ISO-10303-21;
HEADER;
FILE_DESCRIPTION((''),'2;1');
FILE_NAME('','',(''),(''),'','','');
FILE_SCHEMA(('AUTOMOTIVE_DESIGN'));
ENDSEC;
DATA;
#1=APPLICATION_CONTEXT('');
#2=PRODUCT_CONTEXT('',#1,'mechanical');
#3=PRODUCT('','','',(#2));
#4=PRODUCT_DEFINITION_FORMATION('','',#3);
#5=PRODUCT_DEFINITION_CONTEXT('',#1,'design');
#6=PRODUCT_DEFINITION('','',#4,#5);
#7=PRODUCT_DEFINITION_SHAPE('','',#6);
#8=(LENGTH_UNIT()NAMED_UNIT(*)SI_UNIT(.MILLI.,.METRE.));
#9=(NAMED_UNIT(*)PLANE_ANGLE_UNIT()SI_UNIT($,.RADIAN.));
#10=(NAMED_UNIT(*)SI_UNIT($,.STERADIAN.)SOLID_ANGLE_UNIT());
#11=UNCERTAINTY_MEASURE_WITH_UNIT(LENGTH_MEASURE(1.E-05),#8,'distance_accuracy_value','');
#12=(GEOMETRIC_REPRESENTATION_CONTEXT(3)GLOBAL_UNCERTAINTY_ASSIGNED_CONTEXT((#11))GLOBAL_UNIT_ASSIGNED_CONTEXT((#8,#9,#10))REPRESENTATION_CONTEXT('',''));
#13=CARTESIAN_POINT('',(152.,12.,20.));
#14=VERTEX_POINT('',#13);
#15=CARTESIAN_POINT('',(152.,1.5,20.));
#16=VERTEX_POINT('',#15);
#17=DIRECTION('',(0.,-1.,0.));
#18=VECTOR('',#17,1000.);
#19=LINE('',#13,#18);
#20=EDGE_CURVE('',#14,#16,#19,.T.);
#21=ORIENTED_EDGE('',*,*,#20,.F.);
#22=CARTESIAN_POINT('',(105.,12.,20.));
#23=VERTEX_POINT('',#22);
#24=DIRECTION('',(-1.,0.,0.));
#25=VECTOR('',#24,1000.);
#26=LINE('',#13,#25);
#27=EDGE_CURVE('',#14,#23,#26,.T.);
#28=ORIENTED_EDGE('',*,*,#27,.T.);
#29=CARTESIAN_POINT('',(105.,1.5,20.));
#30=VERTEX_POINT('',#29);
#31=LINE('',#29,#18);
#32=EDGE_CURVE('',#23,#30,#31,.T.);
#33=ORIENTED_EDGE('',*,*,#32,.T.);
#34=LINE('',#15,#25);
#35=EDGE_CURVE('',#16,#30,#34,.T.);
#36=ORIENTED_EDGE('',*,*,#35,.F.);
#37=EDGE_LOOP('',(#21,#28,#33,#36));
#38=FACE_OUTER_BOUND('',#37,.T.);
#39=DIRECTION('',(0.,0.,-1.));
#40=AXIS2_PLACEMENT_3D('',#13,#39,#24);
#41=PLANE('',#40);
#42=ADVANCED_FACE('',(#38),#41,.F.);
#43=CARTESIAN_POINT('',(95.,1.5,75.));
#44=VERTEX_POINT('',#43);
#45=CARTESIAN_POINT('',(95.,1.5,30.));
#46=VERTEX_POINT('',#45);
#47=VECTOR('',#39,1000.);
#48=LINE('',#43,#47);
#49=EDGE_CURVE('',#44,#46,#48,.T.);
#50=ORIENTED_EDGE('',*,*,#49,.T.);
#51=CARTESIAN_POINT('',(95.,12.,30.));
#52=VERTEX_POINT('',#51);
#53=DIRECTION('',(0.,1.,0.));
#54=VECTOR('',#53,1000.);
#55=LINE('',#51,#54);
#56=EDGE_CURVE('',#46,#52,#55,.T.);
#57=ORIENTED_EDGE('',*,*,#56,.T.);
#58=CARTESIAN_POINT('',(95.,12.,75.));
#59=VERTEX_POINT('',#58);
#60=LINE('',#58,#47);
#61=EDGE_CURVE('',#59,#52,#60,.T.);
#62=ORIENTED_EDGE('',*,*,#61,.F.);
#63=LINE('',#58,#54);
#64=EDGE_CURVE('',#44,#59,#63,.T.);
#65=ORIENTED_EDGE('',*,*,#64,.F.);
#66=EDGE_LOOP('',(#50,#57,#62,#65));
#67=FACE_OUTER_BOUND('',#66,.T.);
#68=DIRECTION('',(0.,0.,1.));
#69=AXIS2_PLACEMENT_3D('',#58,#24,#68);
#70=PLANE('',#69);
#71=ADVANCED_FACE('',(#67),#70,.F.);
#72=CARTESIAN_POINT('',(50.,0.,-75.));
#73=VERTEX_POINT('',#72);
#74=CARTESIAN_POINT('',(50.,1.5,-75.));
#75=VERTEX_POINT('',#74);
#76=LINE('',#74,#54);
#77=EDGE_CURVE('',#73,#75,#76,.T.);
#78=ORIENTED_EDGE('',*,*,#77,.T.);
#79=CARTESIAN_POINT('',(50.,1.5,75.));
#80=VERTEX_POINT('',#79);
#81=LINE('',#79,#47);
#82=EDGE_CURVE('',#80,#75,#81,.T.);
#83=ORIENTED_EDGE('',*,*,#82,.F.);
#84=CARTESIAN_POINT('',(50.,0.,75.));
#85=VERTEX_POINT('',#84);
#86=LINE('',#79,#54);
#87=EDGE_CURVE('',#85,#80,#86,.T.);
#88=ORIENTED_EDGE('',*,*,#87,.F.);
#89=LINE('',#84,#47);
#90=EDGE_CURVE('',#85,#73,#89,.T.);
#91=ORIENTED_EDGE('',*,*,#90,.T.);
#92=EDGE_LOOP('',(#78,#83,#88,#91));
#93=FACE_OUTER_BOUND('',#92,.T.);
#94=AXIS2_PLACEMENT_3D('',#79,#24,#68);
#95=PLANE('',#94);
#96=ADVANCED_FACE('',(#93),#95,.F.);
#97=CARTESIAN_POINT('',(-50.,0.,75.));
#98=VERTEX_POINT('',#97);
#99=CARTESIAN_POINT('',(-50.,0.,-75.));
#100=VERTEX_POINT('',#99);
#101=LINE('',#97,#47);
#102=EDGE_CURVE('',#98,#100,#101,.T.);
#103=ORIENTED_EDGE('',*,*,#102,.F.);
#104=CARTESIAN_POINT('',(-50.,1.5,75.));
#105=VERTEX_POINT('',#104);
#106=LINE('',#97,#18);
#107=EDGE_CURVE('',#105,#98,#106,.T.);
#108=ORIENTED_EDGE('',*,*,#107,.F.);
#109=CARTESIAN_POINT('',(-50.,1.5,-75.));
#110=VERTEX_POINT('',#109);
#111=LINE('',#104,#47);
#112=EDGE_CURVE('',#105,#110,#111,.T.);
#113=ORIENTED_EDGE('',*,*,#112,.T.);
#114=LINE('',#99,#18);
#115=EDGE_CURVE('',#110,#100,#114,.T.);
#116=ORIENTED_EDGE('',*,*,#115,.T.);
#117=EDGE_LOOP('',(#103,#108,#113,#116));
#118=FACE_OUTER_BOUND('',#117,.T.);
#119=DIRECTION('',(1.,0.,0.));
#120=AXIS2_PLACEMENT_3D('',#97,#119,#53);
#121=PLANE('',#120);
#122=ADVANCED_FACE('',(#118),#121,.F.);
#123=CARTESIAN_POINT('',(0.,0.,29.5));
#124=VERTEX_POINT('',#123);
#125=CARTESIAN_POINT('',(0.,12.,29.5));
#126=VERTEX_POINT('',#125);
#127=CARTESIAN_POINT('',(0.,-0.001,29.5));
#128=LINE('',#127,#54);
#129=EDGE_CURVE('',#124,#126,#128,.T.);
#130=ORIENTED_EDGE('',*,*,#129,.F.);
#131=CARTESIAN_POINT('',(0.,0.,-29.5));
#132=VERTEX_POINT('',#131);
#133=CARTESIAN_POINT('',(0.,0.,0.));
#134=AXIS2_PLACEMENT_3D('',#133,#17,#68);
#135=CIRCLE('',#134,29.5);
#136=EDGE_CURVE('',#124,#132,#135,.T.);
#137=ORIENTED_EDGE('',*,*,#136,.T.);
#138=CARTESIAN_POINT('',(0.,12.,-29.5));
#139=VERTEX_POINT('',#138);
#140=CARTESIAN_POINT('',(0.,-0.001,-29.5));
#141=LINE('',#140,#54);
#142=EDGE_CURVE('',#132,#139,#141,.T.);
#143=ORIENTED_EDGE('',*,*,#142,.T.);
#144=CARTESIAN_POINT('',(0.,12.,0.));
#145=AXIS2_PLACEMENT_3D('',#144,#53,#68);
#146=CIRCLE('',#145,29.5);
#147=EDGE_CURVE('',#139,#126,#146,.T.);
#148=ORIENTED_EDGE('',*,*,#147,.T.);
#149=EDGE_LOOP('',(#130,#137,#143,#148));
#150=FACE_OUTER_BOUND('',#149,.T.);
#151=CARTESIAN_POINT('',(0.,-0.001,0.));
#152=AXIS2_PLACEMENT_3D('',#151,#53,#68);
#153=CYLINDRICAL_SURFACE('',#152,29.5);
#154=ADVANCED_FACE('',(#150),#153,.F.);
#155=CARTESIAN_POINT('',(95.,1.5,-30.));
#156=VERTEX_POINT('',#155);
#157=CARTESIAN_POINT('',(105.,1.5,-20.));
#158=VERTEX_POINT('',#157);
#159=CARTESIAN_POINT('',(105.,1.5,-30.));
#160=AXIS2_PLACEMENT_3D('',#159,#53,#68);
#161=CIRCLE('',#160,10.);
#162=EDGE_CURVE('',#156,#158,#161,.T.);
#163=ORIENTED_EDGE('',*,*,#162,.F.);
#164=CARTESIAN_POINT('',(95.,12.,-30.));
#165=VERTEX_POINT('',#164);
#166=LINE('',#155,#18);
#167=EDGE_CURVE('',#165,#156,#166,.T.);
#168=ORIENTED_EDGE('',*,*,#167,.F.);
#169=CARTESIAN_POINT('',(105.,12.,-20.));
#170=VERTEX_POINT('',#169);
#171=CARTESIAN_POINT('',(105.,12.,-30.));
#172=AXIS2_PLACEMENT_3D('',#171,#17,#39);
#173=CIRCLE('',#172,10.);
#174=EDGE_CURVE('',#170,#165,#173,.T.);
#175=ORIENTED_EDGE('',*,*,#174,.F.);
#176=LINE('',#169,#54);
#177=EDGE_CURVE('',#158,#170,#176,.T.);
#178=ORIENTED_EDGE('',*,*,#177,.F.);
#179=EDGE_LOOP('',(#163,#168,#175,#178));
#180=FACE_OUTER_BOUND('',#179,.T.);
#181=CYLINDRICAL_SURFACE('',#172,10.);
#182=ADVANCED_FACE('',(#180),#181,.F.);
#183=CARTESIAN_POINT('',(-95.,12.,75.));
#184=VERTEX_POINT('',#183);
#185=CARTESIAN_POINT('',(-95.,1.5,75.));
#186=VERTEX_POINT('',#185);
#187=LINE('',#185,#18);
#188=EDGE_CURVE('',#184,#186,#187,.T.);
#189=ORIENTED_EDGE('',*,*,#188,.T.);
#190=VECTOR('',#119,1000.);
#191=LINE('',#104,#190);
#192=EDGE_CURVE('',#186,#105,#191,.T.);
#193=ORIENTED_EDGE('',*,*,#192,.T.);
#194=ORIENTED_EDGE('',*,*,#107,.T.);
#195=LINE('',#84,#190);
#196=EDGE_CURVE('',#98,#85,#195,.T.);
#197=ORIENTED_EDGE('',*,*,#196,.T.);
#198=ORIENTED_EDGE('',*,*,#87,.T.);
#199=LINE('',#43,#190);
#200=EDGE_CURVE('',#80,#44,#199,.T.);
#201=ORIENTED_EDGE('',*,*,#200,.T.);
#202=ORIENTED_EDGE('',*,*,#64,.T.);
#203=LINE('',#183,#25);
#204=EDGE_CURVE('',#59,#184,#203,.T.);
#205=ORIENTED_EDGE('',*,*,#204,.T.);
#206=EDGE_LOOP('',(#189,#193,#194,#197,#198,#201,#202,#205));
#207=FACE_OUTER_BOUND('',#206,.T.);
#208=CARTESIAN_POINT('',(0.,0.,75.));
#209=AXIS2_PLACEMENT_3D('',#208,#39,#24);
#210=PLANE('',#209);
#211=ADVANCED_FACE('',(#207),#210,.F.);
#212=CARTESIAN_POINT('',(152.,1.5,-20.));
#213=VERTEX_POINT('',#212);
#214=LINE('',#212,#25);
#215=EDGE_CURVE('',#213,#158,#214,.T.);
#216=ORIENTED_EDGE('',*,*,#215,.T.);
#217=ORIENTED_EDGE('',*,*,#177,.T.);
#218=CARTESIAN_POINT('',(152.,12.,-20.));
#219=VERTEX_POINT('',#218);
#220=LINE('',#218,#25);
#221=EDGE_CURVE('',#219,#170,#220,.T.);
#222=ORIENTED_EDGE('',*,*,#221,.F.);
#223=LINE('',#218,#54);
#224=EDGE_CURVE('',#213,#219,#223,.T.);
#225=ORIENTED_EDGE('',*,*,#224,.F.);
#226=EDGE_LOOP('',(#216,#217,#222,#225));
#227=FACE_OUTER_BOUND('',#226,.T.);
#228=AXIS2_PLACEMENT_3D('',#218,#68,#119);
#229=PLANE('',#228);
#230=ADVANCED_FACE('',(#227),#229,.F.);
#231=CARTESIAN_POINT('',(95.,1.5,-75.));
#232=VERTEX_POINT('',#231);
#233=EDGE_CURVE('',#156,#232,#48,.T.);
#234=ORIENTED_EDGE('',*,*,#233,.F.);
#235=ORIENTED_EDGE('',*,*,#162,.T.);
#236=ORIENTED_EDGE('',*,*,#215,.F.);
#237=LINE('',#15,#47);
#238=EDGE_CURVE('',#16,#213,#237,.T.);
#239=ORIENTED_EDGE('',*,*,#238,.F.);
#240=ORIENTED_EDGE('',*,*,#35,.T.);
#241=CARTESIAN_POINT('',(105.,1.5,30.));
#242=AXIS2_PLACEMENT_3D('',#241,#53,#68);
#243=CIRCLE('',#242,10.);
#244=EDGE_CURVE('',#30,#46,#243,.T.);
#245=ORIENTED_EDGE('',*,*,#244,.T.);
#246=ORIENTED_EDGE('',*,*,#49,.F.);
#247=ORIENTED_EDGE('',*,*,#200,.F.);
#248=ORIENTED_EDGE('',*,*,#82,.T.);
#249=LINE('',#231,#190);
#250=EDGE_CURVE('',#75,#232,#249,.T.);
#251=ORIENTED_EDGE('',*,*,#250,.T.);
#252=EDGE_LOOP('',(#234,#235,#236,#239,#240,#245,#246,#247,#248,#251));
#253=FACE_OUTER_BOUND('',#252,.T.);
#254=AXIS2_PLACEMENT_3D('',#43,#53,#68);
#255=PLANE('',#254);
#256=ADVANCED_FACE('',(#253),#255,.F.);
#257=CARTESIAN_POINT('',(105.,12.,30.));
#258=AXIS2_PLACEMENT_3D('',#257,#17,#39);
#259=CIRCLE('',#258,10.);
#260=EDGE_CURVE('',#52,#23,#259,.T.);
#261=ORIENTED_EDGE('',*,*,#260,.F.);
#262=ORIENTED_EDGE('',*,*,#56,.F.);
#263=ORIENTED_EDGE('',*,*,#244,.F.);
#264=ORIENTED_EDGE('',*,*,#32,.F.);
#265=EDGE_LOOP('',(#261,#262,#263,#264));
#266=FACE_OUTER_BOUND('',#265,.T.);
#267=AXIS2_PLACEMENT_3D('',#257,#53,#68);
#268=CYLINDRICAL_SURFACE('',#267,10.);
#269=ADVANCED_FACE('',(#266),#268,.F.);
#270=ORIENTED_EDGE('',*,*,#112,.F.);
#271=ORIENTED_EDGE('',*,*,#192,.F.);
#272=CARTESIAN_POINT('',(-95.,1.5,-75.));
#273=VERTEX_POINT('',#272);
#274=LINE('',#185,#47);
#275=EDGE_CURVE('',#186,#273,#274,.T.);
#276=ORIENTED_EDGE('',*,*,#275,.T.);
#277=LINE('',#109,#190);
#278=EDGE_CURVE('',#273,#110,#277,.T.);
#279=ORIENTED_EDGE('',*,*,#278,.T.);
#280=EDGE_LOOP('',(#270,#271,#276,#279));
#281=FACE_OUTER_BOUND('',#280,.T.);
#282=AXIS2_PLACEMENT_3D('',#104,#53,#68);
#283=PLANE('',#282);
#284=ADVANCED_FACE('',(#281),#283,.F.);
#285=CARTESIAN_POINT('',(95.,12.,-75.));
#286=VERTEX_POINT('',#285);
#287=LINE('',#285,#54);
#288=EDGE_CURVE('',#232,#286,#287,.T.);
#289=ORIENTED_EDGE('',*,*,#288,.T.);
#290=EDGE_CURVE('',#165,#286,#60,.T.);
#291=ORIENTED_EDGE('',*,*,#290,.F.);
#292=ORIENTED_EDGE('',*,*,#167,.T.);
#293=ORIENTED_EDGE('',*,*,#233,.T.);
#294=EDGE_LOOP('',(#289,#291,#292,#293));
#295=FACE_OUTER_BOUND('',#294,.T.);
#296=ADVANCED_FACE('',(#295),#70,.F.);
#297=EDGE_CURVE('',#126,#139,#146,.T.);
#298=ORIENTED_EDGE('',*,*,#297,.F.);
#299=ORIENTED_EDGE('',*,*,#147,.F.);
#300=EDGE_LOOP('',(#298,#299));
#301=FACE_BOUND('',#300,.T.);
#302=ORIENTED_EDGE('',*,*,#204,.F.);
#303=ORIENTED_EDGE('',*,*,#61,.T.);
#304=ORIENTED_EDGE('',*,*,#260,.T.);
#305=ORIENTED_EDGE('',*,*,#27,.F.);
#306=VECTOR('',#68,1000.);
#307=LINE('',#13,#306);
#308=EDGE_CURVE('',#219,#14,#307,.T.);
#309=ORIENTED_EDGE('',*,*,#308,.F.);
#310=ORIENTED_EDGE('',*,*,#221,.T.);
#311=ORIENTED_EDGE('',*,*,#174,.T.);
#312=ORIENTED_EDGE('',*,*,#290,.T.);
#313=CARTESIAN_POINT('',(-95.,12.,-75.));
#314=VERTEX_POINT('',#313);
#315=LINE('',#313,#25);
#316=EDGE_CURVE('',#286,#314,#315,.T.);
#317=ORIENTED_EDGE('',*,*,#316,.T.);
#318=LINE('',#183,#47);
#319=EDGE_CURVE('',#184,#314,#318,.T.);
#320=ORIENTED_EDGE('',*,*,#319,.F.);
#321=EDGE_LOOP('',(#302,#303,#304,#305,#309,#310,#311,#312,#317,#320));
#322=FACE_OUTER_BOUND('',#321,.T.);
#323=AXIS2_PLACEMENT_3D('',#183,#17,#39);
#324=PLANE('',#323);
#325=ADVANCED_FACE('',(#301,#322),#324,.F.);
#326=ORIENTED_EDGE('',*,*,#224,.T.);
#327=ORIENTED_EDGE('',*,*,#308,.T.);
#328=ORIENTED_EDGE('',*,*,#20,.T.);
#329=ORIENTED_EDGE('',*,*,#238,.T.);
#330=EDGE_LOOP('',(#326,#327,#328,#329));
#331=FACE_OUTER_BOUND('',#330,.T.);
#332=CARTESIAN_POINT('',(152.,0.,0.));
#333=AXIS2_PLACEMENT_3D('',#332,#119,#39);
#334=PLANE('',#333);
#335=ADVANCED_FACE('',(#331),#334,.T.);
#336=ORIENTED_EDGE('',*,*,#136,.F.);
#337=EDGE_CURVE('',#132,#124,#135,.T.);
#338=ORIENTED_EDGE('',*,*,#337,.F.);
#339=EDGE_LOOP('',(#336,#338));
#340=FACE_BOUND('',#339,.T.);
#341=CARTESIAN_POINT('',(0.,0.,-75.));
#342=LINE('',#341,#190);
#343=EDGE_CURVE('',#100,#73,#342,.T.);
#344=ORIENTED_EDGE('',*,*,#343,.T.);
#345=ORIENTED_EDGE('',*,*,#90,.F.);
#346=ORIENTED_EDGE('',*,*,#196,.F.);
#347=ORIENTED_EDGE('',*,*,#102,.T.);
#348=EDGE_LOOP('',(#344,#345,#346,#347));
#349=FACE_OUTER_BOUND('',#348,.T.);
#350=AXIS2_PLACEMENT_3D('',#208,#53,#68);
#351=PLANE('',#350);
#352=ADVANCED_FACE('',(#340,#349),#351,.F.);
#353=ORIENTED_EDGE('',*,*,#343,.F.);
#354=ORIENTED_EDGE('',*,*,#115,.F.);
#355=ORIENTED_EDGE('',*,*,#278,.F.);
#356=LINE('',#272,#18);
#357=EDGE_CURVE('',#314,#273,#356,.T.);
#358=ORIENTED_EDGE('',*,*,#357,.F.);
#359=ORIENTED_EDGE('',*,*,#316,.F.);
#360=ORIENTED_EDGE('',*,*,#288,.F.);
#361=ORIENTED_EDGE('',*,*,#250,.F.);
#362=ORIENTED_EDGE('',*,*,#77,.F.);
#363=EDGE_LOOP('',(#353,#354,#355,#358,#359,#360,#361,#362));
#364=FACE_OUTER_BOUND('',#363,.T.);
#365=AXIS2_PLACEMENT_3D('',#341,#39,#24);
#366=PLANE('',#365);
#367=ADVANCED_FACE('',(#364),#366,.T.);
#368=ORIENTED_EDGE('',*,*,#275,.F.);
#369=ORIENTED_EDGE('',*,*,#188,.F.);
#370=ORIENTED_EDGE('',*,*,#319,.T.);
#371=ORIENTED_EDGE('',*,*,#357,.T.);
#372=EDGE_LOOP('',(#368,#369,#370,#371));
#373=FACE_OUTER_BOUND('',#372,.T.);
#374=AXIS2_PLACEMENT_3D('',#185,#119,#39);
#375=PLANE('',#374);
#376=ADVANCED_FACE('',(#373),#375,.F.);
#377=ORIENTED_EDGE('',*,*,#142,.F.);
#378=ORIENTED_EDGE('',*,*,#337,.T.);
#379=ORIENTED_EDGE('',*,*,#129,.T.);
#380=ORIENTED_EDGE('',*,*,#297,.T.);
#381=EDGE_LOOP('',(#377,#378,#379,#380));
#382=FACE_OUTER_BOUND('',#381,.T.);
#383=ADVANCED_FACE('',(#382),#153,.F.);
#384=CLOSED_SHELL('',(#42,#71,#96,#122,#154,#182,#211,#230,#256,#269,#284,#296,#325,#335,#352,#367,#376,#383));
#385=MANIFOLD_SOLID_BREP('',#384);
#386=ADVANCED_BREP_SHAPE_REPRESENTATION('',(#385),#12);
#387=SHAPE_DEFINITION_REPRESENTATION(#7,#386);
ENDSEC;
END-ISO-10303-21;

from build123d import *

# Parameters (mm, degrees)
EXTRUDE_1_DEPTH     = 75
CUT_EXTRUDE_1_REACH = 123.631
SKETCH_2_R          = 29.5
SKETCH_4_W          = 40
SKETCH_4_H          = 10.5
EXTRUDE_2_DEPTH     = 57
FILLET_1_R          = 10


with BuildPart() as part:
    # 草图1 → 凸台-拉伸1 (new, symmetric)
    with BuildSketch(Plane.XY):
        Polygon((0, 0), (-50, 0), (-50, 1.5), (-95, 1.5), (-95, 12), (95, 12), (95, 1.5), (50, 1.5), (50, 0), align=None)
    extrude(amount=EXTRUDE_1_DEPTH, both=True)

    # 草图2 → 切除-拉伸1 (cut, up to next)
    with BuildSketch(Plane(origin=(0, 12, 0), x_dir=(1, 0, 0), z_dir=(0, 1, 0)), mode=Mode.PRIVATE) as cut_extrude_1_sk1:
        with Locations(Location((0, 0, 0), (0, 0, 270))):
            Circle(SKETCH_2_R)
    cut_extrude_1_tool1 = extrude(cut_extrude_1_sk1.sketch, amount=-CUT_EXTRUDE_1_REACH, mode=Mode.PRIVATE) & part.part
    add(cut_extrude_1_tool1.solids().sort_by_distance((0, 12, 0))[0], mode=Mode.SUBTRACT)

    # 草图4 → 凸台-拉伸2 (add)
    with BuildSketch(Plane(origin=(95, 0, 0), x_dir=(0, 0, -1), z_dir=(1, 0, 0))):
        with Locations((0, 6.75)):
            Rectangle(SKETCH_4_W, SKETCH_4_H)
    extrude(amount=EXTRUDE_2_DEPTH)

    # 圆角1
    fillet_1_edges = [part.edges().sort_by_distance(p)[0] for p in [
        (95, 6.75, 20),
        (95, 6.75, -20),
    ]]
    fillet(fillet_1_edges, radius=FILLET_1_R)


solid = part.part
